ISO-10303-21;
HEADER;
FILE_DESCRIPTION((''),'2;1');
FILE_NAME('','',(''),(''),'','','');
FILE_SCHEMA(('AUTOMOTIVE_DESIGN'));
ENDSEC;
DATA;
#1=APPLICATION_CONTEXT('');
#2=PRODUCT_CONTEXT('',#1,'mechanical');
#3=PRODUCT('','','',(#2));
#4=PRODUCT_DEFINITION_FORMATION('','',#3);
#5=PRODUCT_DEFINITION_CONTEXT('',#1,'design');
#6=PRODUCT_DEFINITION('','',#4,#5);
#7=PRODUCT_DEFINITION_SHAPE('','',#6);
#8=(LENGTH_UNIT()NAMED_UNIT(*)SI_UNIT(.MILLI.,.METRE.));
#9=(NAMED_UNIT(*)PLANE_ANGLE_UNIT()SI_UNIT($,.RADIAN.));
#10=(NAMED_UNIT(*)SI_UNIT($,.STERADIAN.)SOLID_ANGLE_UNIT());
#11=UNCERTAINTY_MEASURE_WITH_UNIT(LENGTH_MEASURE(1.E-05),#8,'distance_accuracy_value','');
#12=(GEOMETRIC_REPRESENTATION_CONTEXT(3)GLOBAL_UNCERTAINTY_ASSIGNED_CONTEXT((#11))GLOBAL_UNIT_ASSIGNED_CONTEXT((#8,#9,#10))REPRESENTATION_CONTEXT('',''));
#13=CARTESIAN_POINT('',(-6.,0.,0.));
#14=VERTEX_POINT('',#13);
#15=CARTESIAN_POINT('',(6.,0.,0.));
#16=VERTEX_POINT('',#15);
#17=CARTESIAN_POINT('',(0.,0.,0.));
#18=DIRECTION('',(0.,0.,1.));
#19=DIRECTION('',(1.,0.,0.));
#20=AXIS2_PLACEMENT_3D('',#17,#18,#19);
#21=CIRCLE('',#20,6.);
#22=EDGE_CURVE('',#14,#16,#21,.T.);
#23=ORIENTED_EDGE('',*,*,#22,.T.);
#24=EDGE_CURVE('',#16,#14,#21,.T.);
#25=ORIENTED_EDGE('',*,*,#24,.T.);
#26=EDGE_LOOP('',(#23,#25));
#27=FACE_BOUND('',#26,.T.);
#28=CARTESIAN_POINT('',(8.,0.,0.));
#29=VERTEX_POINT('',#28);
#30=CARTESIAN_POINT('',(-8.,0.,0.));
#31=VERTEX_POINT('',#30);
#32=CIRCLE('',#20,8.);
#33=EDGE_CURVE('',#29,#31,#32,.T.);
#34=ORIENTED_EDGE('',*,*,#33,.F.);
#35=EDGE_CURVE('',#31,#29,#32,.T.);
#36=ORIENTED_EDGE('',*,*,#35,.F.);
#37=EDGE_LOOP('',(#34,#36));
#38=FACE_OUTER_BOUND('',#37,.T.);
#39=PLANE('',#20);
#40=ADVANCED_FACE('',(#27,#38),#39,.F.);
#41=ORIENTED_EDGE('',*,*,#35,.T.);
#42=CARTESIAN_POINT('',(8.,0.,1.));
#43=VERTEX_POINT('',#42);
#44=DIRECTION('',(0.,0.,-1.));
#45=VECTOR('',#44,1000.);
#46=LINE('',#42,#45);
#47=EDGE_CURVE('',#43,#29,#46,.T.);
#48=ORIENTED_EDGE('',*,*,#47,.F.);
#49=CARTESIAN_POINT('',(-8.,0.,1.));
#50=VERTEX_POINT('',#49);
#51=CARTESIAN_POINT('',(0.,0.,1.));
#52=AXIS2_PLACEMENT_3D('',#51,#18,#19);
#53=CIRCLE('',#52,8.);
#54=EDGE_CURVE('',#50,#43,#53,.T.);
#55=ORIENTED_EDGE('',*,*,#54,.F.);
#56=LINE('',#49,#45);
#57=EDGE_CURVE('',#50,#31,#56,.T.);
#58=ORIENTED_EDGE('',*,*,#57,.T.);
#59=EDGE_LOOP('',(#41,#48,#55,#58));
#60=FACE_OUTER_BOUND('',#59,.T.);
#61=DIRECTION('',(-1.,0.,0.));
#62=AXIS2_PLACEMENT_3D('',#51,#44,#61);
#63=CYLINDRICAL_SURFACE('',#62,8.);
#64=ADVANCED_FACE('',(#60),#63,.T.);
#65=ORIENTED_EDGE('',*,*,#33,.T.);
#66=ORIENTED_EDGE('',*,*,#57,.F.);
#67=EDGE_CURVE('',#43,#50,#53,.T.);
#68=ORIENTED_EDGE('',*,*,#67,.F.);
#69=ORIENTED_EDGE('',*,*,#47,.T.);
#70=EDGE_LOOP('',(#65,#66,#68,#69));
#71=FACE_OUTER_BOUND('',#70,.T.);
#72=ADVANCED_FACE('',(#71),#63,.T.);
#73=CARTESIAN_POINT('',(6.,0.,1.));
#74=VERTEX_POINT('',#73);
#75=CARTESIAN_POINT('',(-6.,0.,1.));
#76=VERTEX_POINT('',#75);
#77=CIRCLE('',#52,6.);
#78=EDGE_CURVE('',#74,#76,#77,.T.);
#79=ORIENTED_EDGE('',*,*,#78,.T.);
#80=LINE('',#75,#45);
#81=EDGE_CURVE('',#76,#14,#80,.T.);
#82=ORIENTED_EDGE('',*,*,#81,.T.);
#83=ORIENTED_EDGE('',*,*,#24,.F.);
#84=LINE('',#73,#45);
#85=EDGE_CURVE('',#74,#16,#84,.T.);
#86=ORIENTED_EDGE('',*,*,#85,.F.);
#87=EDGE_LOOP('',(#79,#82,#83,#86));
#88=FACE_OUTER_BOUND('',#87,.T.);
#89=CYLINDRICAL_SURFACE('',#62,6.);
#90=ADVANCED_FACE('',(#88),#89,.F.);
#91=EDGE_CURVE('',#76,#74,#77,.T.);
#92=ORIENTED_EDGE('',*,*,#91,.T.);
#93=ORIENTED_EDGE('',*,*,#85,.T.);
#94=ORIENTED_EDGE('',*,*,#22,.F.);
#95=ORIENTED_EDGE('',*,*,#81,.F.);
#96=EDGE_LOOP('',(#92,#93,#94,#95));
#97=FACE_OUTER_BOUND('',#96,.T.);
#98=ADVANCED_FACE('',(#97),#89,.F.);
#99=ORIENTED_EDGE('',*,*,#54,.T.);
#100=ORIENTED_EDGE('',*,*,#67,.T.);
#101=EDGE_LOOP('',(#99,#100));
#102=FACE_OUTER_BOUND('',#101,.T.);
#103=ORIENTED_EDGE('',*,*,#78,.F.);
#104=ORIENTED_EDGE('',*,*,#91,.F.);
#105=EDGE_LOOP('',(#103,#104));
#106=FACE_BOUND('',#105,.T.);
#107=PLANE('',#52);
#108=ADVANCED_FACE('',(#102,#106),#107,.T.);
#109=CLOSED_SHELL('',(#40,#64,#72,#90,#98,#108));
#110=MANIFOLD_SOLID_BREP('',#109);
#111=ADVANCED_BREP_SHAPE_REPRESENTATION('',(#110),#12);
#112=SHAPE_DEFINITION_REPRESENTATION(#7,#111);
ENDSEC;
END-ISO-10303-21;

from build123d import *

# Parameters (mm, degrees)
SKETCH1_R           = 8
SKETCH1_R_2         = 6
BOSS_EXTRUDE1_DEPTH = 1


with BuildPart() as part:
    # Sketch1 → Boss-Extrude1 (new body)
    with BuildSketch(Plane.XY):
        Circle(SKETCH1_R)
        Circle(SKETCH1_R_2, mode=Mode.SUBTRACT)
    extrude(amount=BOSS_EXTRUDE1_DEPTH)


solid = part.part
